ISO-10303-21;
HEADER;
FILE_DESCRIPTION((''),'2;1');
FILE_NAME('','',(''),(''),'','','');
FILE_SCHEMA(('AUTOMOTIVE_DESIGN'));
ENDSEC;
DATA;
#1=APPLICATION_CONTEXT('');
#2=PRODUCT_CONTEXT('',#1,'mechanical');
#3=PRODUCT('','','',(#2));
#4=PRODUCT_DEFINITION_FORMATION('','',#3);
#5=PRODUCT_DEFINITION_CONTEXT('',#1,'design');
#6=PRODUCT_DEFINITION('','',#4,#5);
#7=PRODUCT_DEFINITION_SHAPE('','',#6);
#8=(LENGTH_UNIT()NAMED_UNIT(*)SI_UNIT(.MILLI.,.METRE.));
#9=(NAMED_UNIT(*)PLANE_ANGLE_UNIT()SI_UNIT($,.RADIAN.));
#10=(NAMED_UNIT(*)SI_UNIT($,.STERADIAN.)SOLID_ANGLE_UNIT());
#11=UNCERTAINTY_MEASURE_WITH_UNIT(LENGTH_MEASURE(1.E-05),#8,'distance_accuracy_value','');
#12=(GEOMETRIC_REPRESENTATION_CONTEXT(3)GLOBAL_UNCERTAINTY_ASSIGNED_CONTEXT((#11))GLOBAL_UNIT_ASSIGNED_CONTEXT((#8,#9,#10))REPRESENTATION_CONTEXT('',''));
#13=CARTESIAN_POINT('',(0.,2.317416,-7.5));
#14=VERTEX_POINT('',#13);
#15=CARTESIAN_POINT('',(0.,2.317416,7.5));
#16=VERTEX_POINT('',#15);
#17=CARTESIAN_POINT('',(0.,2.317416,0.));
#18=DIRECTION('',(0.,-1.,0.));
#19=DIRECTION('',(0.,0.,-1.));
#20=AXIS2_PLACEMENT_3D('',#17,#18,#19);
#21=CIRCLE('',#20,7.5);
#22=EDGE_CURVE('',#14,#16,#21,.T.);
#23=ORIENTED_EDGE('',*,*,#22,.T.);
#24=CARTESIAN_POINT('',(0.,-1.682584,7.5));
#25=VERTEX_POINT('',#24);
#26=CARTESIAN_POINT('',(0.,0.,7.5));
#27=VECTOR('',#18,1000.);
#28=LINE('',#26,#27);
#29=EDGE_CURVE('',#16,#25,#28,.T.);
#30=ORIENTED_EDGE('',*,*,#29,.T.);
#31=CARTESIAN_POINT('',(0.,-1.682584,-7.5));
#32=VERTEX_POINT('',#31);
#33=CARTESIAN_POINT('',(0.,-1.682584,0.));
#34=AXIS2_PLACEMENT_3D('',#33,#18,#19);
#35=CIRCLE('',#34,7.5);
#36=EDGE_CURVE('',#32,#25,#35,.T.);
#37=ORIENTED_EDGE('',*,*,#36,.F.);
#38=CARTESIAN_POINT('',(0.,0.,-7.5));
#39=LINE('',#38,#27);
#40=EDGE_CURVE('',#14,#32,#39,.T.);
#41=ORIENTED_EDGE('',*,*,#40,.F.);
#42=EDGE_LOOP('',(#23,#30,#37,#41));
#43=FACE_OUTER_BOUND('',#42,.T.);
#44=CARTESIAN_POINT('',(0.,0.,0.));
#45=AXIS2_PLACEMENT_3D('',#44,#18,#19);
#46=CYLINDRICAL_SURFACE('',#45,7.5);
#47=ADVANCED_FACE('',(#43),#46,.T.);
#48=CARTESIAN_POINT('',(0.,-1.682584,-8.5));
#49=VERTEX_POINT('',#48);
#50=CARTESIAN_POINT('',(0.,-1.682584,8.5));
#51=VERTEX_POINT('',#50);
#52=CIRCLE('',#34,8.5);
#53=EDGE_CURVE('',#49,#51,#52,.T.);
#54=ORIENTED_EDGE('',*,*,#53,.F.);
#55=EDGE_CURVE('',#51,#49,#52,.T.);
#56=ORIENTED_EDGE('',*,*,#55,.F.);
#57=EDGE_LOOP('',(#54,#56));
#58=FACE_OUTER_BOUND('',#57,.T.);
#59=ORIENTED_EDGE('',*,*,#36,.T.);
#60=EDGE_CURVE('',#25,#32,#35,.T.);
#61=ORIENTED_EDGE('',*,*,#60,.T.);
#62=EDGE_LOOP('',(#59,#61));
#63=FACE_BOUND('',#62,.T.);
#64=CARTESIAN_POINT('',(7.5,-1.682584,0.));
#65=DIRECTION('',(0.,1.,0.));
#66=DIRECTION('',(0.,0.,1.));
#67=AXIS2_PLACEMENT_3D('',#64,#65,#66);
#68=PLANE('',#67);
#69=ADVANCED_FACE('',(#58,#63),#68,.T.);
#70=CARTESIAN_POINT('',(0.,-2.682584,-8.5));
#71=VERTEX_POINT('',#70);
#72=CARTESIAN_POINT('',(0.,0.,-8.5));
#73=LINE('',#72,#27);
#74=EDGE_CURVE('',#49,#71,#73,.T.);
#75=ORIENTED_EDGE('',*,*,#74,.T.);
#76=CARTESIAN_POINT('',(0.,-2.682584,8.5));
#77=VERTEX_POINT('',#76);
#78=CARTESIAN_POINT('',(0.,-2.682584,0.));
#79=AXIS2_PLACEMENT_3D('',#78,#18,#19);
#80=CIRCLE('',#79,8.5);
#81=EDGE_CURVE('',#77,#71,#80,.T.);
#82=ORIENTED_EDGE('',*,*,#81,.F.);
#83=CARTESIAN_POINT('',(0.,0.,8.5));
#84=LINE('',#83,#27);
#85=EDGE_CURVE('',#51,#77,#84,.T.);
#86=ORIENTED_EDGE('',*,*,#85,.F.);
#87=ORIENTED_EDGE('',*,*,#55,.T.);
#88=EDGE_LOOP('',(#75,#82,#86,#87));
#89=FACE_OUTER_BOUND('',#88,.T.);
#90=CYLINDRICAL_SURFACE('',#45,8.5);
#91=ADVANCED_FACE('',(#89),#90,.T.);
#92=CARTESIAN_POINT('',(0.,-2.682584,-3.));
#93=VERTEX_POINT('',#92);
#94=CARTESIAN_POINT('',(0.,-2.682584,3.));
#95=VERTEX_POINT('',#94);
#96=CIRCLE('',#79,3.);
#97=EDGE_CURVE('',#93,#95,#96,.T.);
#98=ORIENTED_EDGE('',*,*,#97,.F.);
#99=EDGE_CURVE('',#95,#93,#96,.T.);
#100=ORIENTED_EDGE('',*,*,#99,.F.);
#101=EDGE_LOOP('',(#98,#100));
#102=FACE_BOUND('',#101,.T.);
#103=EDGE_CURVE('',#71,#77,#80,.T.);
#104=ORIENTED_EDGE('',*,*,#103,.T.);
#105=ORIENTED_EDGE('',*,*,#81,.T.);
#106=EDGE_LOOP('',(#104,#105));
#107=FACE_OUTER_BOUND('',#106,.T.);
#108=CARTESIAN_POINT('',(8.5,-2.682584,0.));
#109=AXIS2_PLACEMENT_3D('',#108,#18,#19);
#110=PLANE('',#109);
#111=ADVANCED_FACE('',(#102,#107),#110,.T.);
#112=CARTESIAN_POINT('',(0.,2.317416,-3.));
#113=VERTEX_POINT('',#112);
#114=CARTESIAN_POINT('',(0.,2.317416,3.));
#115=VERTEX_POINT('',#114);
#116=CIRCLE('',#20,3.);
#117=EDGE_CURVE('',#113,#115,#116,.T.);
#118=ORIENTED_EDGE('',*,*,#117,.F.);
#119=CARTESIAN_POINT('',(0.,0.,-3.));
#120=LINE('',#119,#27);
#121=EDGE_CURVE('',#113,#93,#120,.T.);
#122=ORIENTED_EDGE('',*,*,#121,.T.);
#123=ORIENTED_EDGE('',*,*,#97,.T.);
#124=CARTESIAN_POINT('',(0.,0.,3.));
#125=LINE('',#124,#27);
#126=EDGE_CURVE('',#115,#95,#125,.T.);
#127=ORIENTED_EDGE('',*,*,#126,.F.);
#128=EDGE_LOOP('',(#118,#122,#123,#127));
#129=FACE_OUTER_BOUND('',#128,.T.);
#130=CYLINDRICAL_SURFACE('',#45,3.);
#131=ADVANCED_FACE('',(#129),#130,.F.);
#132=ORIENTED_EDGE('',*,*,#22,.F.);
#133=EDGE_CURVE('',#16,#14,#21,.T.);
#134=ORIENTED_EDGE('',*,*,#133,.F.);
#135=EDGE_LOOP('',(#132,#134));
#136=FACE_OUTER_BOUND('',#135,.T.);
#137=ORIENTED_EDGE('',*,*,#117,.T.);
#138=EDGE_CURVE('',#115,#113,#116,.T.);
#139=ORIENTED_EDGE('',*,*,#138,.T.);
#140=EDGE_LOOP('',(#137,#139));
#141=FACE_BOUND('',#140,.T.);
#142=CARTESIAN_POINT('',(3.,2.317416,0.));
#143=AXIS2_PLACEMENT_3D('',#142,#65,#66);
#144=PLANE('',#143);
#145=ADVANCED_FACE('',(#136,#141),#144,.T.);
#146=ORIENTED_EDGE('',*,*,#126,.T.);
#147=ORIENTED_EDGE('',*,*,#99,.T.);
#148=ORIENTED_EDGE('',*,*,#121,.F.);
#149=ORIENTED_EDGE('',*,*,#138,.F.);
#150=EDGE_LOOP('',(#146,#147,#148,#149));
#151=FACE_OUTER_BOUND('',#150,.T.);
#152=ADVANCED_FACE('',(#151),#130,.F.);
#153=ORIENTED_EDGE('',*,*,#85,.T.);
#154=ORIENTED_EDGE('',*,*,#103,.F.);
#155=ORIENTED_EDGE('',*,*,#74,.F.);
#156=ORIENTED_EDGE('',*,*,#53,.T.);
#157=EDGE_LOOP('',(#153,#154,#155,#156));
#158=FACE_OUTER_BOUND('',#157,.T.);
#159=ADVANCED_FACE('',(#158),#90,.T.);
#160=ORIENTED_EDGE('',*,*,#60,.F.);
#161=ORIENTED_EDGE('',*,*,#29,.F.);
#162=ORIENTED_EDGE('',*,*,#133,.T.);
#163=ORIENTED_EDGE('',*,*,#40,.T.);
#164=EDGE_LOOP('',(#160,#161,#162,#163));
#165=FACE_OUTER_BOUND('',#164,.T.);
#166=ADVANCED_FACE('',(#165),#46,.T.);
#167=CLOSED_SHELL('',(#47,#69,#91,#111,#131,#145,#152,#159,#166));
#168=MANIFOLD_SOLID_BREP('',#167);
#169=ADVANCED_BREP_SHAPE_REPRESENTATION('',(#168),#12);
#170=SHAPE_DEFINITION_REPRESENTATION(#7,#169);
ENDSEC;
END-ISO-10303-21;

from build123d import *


with BuildPart() as part:
    # 草图1 → 旋转1 (revolve)
    with BuildSketch(Plane.XY, mode=Mode.PRIVATE) as revolve_1_sk:
        Polygon((3, 2.31741573), (7.5, 2.31741573), (7.5, -1.68258427), (8.5, -1.68258427), (8.5, -2.68258427), (3, -2.68258427), align=None)
    revolve(revolve_1_sk.sketch.rotate(Axis((0, 0, 0), (0, 1, 0)), 90), axis=Axis((0, 0, 0), (0, 1, 0)))


solid = part.part
